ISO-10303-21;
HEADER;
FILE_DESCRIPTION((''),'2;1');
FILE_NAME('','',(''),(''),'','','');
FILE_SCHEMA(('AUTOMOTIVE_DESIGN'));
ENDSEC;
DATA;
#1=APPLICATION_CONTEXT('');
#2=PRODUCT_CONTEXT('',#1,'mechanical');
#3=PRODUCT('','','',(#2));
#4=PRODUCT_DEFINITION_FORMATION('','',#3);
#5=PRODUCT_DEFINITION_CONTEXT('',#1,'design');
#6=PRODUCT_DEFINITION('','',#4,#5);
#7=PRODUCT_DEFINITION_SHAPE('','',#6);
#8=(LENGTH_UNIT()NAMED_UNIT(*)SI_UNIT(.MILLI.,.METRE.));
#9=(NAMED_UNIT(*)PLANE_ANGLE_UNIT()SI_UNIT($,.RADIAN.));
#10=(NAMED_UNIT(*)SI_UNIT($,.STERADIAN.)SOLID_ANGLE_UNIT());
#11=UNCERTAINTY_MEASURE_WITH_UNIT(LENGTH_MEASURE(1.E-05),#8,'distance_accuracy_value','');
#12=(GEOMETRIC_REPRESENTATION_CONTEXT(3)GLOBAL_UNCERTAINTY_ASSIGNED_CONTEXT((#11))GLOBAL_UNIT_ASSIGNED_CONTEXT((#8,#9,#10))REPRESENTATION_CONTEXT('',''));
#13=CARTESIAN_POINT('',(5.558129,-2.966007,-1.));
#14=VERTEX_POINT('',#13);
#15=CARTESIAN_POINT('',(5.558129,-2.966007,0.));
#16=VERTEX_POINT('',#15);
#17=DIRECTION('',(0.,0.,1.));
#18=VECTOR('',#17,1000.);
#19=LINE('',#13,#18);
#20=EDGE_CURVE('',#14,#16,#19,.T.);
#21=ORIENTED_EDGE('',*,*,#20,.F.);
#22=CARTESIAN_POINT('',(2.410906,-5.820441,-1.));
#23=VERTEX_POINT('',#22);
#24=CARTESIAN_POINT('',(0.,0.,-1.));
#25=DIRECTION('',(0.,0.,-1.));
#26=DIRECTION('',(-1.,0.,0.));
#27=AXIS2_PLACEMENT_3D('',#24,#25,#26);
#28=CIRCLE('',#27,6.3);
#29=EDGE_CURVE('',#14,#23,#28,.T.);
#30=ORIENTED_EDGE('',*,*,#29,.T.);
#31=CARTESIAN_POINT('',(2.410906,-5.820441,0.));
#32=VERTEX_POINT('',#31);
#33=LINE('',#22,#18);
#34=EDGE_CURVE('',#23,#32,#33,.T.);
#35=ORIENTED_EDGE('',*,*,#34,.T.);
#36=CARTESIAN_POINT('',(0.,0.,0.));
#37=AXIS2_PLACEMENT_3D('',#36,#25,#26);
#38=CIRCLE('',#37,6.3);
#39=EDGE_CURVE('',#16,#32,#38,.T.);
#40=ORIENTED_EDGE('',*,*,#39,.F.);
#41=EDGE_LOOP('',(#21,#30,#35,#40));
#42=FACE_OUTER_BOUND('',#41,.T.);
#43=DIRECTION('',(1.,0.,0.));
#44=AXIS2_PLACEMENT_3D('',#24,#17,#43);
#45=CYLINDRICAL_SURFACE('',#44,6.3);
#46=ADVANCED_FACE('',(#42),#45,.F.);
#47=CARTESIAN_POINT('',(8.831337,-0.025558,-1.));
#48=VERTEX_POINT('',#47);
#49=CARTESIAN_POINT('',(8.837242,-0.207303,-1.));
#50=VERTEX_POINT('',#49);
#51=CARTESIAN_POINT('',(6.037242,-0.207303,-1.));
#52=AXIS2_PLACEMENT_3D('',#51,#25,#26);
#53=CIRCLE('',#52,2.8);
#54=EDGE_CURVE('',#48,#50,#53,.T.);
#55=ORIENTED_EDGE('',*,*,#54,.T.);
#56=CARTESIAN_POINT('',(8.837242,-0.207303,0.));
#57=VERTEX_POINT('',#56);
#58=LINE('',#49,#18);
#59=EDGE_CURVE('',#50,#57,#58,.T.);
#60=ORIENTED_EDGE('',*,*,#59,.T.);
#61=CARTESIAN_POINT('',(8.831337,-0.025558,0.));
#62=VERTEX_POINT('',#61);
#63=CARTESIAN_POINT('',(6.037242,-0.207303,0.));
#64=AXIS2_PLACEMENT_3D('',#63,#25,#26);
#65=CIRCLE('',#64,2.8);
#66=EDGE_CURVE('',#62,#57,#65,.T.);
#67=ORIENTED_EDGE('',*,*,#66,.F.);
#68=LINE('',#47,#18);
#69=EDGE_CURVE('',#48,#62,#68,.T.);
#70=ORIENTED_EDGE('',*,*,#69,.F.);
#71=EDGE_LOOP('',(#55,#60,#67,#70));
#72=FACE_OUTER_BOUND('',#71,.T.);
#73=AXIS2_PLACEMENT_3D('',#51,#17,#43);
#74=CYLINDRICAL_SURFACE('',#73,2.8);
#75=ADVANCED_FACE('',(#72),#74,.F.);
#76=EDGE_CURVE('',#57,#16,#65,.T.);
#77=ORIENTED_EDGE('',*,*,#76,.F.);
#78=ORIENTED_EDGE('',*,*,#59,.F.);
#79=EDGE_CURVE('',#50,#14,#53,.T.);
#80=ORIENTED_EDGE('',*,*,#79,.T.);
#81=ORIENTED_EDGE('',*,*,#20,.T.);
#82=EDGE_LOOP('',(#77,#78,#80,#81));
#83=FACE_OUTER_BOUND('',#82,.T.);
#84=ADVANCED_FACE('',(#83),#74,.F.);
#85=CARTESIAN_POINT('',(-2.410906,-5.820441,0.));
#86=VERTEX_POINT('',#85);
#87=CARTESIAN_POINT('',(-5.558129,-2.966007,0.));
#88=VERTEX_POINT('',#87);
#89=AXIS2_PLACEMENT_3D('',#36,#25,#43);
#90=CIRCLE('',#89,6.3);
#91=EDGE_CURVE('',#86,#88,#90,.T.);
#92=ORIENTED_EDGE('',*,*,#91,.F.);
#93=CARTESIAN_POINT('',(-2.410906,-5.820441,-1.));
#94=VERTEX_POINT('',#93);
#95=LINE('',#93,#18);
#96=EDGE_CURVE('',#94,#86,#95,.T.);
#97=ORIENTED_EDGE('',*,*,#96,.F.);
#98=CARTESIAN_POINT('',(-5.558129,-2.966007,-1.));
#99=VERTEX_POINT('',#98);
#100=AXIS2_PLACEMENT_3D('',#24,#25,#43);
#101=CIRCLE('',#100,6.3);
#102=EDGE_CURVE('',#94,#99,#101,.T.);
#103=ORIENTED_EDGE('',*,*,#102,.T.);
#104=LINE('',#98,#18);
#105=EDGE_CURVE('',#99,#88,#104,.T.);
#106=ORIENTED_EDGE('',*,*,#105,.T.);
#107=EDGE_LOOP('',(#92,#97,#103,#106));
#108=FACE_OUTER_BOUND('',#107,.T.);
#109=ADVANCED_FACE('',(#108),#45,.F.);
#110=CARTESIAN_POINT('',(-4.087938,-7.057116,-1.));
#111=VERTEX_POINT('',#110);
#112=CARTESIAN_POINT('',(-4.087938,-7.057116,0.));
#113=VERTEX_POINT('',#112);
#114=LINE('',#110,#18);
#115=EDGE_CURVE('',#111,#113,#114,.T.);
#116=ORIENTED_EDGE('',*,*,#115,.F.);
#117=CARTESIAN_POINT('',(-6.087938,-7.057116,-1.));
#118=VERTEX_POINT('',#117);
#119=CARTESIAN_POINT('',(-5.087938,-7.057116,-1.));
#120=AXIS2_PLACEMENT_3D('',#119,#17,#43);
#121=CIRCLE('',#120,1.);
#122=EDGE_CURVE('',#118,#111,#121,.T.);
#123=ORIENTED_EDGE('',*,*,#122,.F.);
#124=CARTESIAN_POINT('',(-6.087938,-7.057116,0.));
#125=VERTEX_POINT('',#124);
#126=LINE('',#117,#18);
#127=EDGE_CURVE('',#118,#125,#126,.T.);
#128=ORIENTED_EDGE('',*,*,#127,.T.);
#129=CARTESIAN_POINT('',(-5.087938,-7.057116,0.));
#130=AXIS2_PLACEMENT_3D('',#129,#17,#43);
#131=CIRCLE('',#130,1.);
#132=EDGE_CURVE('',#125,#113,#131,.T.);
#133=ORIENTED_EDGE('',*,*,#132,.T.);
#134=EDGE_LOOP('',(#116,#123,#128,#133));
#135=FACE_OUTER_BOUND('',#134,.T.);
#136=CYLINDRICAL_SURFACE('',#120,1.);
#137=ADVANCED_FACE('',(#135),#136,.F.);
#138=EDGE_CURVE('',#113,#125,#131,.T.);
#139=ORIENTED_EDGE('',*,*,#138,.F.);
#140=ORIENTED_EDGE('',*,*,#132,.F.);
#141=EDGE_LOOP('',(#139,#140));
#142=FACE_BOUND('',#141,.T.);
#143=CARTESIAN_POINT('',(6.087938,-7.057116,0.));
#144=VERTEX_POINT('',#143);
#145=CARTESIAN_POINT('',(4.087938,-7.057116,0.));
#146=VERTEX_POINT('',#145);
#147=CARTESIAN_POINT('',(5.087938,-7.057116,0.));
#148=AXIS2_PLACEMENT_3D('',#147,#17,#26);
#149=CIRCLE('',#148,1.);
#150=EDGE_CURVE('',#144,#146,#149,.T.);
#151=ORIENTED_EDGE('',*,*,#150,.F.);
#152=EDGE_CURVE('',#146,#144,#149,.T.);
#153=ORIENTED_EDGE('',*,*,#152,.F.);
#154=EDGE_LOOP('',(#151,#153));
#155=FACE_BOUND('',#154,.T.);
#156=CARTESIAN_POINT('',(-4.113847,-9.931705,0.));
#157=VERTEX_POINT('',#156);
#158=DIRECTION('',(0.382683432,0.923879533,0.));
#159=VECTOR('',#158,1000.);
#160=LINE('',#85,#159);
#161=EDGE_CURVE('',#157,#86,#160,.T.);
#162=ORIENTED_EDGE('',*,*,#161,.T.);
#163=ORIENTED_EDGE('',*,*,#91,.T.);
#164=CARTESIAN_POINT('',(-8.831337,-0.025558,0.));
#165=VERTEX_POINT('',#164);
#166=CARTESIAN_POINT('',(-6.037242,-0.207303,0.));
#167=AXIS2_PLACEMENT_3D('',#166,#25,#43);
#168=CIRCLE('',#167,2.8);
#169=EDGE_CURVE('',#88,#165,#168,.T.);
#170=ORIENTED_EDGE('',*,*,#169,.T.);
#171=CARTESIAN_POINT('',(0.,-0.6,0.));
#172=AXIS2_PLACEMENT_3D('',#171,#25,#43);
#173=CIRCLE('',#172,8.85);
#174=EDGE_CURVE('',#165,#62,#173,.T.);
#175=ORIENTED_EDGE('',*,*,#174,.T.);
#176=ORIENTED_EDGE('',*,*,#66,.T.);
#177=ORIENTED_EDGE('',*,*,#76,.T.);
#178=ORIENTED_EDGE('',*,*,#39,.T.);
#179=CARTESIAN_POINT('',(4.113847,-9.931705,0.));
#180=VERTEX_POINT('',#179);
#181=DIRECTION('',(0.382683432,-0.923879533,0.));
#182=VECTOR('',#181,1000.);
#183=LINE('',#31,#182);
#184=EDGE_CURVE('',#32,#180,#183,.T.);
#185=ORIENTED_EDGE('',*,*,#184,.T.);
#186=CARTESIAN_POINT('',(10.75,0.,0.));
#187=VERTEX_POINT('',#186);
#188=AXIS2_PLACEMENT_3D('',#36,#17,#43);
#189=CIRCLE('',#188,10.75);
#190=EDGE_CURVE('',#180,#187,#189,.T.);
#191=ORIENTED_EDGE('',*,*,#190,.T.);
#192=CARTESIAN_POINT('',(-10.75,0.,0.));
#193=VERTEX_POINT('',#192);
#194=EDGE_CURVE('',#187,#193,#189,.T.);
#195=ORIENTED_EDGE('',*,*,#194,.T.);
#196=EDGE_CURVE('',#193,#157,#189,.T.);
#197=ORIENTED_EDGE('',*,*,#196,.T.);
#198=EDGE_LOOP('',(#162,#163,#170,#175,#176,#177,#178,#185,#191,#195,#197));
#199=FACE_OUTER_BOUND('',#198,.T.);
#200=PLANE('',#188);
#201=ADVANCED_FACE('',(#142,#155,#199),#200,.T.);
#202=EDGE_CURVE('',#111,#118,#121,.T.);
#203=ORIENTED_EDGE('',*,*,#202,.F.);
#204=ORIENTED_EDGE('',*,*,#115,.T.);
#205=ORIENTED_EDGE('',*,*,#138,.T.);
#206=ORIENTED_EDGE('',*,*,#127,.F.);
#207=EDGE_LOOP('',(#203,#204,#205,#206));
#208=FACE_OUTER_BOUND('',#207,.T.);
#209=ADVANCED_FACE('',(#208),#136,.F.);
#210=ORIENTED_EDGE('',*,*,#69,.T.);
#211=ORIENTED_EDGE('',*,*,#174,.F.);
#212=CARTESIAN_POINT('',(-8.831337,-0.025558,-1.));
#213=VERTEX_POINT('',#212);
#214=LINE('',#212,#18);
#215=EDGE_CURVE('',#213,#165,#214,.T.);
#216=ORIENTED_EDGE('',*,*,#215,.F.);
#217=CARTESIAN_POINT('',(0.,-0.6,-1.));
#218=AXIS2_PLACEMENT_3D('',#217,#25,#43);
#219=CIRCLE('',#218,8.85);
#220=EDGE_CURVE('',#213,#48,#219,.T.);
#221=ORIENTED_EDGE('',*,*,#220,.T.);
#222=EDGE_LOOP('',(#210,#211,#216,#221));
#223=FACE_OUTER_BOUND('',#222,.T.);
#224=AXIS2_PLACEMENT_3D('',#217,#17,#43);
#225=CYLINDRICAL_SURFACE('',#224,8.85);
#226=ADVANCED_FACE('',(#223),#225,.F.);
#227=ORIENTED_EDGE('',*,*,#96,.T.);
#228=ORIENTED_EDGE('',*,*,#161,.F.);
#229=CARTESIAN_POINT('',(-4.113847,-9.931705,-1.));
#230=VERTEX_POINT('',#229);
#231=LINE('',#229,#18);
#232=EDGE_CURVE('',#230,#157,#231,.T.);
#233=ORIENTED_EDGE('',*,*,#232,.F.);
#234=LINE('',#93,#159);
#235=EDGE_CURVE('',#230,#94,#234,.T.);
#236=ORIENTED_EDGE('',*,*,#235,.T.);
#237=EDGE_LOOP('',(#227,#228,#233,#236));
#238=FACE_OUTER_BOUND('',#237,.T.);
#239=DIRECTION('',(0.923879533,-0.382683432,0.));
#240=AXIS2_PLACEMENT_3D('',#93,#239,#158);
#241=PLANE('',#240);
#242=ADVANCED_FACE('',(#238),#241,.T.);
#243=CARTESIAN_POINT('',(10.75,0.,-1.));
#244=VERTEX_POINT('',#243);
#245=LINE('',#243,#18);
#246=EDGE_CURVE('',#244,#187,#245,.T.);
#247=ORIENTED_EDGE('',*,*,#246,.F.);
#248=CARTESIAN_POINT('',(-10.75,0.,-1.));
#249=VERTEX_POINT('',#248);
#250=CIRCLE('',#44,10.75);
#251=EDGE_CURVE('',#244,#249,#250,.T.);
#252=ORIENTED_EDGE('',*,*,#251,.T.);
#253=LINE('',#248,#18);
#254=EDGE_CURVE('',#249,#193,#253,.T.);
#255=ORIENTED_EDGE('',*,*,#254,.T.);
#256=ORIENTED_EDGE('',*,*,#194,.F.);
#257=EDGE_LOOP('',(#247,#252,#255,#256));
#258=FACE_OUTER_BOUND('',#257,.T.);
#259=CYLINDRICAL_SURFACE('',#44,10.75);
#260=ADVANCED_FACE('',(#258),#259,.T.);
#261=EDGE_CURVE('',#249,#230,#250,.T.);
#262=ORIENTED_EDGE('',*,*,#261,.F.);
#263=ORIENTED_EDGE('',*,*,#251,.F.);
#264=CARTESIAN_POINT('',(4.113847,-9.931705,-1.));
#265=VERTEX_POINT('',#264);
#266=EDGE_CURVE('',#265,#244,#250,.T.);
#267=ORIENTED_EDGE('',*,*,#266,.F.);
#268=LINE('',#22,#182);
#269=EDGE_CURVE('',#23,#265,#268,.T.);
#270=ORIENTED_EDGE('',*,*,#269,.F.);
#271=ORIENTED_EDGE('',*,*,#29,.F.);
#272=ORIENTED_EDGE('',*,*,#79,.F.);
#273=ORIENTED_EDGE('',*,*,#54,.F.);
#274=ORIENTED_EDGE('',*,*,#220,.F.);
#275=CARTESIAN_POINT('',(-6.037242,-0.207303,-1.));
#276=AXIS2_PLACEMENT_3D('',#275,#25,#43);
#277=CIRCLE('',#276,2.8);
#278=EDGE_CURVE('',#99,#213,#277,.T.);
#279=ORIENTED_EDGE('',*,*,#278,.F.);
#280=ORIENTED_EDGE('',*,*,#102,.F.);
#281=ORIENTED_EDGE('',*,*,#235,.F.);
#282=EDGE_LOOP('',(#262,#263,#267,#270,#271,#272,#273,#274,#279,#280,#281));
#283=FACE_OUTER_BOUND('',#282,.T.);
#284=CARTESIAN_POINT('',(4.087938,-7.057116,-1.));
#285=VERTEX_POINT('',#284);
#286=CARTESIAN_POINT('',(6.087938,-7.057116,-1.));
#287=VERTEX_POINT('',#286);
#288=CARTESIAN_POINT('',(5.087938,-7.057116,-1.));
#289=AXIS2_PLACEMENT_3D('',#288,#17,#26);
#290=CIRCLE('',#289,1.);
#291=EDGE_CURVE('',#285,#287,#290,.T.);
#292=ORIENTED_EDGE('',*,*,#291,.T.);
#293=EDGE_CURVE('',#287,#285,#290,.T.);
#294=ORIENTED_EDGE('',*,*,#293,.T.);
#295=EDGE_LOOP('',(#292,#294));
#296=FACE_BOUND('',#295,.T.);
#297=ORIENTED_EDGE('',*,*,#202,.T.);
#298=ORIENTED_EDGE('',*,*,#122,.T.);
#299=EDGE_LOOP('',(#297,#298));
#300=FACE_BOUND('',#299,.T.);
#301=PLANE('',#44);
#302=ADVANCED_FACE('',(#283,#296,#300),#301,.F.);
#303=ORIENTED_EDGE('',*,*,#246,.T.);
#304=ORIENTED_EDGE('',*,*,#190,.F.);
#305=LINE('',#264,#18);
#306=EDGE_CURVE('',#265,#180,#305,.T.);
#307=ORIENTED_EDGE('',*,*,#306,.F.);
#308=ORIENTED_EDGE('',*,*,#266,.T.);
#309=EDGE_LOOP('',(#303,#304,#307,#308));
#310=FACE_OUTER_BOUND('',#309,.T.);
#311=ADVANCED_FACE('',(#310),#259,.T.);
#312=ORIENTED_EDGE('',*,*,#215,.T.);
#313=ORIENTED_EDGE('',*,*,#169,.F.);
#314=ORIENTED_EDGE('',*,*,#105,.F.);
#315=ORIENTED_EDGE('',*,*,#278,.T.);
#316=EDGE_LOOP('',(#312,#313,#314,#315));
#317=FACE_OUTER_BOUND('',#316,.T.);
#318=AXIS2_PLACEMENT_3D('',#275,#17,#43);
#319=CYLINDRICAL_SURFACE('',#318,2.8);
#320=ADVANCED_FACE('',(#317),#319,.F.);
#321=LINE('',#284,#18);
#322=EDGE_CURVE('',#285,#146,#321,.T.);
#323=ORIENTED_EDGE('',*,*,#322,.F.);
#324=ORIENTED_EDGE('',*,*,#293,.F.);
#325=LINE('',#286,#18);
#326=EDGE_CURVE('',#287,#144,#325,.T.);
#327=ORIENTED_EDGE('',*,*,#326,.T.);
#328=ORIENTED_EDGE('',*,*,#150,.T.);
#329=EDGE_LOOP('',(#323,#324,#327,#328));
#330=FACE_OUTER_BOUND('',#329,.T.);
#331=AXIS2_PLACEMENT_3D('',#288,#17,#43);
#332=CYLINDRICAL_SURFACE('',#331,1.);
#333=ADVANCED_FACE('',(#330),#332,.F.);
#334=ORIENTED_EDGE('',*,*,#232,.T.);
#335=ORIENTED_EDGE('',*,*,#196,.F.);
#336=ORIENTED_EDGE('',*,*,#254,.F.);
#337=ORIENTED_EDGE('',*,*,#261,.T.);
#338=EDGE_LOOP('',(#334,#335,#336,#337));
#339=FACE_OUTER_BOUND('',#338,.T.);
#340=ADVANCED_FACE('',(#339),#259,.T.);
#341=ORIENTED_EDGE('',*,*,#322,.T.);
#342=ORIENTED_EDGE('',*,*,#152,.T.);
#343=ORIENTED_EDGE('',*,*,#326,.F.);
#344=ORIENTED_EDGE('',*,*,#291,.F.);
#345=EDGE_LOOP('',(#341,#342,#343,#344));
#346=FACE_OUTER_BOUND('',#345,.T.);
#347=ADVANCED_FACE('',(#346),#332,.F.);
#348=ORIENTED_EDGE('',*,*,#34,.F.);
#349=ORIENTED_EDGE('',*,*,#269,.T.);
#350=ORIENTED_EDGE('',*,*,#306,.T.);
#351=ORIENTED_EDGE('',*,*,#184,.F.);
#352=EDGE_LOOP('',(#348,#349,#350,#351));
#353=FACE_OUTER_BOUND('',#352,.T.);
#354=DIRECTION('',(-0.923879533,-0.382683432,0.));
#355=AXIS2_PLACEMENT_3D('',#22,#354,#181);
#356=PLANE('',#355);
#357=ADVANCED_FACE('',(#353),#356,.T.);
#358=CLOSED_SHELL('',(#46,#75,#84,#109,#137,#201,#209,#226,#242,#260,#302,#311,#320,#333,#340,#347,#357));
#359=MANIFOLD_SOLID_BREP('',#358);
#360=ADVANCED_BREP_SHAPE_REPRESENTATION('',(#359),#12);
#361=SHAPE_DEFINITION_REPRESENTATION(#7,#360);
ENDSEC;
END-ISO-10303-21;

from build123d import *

# Parameters (mm, degrees)
SKETCH1_R  = 1
BODY_DEPTH = 1


with BuildPart() as part:
    # Sketch1 → Body (new body)
    with BuildSketch(Plane.XY):
        with BuildLine():
            Line((-2.410905624, -5.820441055), (-4.113846898, -9.931704974))
            ThreePointArc((-4.113846898, -9.931704974), (0, 10.75), (4.113846898, -9.931704974))
            Line((4.113846898, -9.931704974), (2.410905624, -5.820441055))
            ThreePointArc((2.410905624, -5.820441055), (4.232413877, -4.666548272), (5.558129248, -2.966007293))
            ThreePointArc((5.558129248, -2.966007293), (7.908430264, -2.290246226), (8.83133721, -0.025558466))
            ThreePointArc((8.83133721, -0.025558466), (0, 8.25), (-8.83133721, -0.025558466))
            ThreePointArc((-8.83133721, -0.025558466), (-7.908430264, -2.290246226), (-5.558129248, -2.966007293))
            ThreePointArc((-5.558129248, -2.966007293), (-4.232413877, -4.666548272), (-2.410905624, -5.820441055))
        make_face()
        with Locations(Location((5.087937676, -7.057116281, 0), (0, 0, 180))):
            Circle(SKETCH1_R, mode=Mode.SUBTRACT)
        with Locations((-5.087937676, -7.057116281)):
            Circle(SKETCH1_R, mode=Mode.SUBTRACT)
    extrude(amount=-BODY_DEPTH)


solid = part.part
